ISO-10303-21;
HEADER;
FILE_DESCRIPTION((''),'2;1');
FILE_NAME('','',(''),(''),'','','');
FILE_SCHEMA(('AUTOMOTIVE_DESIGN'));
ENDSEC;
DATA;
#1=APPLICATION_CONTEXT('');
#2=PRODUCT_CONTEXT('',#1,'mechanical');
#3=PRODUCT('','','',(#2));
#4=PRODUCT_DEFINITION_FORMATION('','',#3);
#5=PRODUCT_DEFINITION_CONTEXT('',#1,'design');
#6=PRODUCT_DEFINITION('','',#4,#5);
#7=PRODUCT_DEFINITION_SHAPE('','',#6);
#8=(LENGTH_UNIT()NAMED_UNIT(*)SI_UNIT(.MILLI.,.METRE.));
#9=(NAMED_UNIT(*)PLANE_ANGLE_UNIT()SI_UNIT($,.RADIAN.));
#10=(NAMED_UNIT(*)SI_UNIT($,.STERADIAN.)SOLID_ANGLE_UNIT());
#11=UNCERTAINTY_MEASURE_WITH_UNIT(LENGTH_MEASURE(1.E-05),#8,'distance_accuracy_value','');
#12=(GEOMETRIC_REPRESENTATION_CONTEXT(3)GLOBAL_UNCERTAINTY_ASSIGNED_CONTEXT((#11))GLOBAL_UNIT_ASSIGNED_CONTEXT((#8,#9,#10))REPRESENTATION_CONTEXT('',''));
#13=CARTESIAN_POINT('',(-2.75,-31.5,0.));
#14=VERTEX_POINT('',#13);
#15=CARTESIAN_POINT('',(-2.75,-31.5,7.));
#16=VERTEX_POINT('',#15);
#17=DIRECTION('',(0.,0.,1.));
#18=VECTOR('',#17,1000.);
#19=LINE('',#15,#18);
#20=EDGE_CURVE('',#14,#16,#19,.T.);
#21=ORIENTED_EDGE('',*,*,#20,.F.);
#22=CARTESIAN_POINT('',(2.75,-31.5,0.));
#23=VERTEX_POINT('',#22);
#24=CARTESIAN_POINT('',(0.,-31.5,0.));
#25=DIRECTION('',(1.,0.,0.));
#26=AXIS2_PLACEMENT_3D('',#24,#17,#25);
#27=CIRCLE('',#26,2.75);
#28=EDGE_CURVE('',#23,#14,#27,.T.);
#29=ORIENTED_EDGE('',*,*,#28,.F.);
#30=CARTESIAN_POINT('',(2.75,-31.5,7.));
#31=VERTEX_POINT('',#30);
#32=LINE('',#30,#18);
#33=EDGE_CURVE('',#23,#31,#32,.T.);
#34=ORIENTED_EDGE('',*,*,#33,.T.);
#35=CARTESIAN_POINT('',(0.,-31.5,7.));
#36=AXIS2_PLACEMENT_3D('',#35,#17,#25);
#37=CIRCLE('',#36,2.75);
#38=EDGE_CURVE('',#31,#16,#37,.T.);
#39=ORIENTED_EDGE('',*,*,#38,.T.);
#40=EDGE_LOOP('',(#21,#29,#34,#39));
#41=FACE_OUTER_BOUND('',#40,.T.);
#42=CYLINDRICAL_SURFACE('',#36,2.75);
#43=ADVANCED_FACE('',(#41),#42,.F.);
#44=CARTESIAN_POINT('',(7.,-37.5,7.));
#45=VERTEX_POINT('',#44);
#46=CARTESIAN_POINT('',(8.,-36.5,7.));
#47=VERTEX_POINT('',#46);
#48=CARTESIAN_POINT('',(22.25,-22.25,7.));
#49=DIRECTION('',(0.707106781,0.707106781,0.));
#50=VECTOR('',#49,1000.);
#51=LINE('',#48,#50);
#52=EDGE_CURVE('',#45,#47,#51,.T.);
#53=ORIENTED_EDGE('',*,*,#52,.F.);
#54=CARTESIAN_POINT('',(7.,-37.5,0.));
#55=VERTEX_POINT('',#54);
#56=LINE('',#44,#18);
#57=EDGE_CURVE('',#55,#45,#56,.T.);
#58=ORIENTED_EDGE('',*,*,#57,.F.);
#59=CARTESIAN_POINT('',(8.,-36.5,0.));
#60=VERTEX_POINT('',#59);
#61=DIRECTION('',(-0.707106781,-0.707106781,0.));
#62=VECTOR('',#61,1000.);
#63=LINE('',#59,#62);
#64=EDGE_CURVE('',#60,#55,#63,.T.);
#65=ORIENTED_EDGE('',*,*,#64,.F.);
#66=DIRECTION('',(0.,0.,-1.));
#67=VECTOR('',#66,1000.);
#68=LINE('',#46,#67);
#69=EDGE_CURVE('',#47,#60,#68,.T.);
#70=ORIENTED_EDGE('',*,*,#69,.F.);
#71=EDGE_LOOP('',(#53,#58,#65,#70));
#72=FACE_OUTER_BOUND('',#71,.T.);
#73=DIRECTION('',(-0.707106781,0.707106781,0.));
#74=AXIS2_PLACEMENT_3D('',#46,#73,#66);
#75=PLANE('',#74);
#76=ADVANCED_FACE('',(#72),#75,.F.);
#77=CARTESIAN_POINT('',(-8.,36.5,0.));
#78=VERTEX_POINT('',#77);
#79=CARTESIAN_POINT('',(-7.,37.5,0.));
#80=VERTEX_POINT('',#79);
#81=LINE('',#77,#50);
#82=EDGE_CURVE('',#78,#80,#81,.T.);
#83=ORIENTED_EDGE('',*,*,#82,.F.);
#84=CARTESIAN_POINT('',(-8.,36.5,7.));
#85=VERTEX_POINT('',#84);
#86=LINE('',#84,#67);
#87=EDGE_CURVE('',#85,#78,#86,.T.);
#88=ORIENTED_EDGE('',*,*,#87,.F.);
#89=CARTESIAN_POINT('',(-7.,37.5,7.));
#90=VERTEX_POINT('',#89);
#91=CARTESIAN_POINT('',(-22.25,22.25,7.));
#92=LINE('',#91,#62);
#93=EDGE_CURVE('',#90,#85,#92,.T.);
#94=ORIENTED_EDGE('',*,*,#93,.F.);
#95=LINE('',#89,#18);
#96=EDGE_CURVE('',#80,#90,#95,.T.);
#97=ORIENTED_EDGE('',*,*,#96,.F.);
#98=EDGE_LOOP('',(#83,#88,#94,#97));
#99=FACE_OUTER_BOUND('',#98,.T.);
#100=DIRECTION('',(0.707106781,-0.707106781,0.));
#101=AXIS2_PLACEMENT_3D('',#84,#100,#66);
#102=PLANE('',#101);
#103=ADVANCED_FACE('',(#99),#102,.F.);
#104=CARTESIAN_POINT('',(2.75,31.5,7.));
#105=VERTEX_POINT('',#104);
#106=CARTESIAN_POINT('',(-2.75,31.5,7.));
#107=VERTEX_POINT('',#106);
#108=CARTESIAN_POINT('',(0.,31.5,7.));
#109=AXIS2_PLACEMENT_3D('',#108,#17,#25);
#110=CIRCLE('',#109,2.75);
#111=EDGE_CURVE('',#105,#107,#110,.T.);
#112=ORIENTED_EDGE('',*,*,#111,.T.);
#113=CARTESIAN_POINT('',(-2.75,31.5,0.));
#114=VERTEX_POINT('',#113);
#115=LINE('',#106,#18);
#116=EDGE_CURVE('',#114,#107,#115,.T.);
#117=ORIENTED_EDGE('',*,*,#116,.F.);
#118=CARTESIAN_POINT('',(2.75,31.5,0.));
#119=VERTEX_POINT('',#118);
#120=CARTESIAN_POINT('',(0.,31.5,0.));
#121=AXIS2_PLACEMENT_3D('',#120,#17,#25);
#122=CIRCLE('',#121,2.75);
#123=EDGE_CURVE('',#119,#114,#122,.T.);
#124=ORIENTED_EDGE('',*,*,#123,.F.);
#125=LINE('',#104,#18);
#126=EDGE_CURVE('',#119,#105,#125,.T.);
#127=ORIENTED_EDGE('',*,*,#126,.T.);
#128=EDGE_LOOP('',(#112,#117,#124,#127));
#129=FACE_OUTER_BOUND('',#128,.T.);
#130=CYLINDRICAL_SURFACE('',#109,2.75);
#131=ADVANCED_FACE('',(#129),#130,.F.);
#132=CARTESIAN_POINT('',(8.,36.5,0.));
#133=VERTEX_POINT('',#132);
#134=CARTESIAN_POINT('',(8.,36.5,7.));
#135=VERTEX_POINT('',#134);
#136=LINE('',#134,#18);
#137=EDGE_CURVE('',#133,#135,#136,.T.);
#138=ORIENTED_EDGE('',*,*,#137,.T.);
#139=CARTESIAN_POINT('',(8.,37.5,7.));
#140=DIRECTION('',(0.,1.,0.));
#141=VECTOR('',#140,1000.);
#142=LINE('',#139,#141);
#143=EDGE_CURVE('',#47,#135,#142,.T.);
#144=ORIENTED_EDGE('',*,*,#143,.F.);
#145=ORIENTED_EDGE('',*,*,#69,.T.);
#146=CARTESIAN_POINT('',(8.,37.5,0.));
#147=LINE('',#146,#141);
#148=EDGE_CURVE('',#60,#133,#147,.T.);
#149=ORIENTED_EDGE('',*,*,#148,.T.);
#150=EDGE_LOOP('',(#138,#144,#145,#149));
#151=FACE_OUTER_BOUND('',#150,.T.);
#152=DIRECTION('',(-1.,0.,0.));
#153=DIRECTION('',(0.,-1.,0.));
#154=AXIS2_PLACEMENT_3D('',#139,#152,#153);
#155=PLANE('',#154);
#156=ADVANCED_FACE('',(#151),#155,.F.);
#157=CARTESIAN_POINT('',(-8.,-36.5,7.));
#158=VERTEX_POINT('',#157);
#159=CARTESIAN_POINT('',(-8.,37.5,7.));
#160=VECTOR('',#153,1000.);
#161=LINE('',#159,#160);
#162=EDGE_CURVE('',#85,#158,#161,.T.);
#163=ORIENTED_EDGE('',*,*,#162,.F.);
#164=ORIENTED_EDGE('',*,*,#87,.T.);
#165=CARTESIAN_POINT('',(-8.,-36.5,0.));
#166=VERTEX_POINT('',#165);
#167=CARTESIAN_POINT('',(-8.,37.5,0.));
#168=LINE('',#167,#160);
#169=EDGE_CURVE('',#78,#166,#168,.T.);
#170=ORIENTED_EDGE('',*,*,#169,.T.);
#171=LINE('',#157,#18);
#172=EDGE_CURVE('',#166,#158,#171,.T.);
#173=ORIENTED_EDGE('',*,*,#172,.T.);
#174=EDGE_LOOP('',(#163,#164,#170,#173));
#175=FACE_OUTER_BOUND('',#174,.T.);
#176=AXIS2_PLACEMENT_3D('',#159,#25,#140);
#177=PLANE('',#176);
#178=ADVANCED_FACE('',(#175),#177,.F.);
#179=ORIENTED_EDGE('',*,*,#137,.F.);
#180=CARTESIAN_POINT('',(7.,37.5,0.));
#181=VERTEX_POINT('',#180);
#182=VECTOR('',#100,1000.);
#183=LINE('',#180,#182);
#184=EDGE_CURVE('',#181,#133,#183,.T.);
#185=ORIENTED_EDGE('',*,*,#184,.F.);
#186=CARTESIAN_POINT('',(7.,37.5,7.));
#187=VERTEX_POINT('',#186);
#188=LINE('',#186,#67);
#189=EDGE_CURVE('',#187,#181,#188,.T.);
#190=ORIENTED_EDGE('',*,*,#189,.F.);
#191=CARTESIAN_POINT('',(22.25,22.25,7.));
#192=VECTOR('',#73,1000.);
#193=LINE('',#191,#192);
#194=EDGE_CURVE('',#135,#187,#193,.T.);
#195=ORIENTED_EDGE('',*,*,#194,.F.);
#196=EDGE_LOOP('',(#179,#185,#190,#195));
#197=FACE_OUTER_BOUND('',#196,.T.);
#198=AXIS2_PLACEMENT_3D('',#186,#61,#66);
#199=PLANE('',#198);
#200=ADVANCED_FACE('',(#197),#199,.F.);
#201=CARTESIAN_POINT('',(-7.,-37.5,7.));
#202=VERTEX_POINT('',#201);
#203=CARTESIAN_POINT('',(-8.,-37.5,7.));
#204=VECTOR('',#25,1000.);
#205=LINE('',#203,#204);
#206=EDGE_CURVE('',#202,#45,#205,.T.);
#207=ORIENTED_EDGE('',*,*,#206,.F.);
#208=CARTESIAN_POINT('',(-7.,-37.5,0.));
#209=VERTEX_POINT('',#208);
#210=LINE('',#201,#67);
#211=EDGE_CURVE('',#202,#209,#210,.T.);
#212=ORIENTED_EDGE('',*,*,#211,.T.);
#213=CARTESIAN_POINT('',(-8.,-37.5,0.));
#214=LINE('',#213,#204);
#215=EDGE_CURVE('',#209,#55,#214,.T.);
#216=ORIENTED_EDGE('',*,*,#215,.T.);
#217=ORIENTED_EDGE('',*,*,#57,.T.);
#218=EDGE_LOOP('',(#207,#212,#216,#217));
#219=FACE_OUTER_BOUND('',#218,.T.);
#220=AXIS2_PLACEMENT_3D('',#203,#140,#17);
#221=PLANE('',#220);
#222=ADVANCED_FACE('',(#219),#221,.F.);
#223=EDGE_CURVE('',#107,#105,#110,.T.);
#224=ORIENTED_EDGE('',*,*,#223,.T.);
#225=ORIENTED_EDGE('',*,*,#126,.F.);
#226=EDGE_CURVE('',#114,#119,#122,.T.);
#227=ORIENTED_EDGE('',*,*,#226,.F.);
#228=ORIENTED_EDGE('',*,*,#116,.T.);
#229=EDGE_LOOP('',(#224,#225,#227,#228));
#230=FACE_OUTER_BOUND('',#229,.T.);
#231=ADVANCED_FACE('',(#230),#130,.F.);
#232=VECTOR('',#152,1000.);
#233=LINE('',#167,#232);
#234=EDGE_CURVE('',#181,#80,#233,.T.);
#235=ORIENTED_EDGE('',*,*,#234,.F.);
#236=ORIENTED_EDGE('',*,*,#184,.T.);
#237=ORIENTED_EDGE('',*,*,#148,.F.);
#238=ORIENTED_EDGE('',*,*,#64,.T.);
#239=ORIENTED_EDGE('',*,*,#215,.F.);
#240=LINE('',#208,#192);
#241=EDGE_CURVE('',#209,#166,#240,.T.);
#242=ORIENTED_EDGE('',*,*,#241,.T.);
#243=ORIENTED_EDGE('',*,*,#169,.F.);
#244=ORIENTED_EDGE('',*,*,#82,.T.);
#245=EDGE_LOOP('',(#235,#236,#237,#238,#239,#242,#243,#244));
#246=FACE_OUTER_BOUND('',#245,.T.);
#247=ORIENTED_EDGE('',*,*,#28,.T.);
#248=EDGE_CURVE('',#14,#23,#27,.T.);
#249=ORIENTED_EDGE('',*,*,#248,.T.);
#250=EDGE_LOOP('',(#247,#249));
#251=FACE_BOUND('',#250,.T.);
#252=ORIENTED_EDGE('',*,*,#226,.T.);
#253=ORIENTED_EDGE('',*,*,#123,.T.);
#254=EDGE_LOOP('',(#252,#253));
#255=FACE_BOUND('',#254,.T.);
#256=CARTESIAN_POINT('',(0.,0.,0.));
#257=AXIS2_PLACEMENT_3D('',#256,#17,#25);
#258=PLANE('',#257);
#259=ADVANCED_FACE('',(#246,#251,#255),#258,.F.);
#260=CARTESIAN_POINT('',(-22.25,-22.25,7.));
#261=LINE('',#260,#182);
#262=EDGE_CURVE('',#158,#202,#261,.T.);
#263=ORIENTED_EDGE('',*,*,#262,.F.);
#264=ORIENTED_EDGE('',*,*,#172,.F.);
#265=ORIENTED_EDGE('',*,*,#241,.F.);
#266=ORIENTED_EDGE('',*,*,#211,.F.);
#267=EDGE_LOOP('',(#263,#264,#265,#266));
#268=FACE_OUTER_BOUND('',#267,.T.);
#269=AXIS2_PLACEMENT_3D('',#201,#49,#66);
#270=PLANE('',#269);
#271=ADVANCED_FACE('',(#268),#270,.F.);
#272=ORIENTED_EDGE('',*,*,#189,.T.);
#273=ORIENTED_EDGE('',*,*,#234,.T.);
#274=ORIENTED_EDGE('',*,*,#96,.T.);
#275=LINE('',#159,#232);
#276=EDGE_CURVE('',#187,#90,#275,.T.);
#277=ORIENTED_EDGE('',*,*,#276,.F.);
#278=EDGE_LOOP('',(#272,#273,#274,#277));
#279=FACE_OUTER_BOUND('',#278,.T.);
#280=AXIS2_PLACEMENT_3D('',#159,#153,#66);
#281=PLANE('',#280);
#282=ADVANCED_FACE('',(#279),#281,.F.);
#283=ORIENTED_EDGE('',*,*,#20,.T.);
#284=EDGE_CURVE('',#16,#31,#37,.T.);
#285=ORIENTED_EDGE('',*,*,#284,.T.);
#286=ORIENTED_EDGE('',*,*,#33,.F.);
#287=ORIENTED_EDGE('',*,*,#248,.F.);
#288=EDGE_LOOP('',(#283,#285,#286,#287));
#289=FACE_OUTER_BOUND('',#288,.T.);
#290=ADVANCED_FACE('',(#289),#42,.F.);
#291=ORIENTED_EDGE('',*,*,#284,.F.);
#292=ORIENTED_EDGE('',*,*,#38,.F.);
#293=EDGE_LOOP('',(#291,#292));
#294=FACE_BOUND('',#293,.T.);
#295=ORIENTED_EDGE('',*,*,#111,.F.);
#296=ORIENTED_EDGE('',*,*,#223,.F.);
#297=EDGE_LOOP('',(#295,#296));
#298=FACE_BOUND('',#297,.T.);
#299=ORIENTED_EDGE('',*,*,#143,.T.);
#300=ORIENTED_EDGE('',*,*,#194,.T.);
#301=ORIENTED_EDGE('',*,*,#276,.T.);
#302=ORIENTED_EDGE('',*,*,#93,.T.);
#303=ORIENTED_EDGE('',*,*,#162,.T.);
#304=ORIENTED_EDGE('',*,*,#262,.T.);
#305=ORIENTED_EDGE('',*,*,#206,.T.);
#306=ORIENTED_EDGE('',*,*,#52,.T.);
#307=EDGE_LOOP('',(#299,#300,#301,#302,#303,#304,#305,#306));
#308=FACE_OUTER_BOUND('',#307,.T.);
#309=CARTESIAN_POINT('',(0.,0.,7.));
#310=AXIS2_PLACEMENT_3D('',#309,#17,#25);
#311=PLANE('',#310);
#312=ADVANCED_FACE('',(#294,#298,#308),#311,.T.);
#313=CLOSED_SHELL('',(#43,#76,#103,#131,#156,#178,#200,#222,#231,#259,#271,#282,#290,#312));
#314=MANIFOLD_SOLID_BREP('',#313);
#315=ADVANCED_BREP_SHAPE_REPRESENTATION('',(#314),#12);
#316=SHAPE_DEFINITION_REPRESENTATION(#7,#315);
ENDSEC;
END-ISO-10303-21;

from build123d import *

# Parameters (mm, degrees)
SKETCH1_W            = 16
SKETCH1_H            = 75
BOSS_EXTRUDE1_DEPTH  = 7
CHAMFER5_SIZE        = 1
M5_CLEARANCE_HOLE1_D = 5.5


with BuildPart() as part:
    # Sketch1 → Boss-Extrude1 (new body)
    with BuildSketch(Plane.XY):
        Rectangle(SKETCH1_W, SKETCH1_H)
    extrude(amount=BOSS_EXTRUDE1_DEPTH)

    # Chamfer5
    chamfer5_edges = [part.edges().sort_by_distance(p)[0] for p in [
        (8, -37.5, 3.5),
        (-8, -37.5, 3.5),
        (-8, 37.5, 3.5),
        (8, 37.5, 3.5),
    ]]
    chamfer(chamfer5_edges, length=CHAMFER5_SIZE)

    # M5 Clearance Hole1 (through all)
    with Locations(Plane.XY.offset(7)):
        with Locations((0, 31.5), (0, -31.5)):
            Hole(M5_CLEARANCE_HOLE1_D / 2)


solid = part.part
